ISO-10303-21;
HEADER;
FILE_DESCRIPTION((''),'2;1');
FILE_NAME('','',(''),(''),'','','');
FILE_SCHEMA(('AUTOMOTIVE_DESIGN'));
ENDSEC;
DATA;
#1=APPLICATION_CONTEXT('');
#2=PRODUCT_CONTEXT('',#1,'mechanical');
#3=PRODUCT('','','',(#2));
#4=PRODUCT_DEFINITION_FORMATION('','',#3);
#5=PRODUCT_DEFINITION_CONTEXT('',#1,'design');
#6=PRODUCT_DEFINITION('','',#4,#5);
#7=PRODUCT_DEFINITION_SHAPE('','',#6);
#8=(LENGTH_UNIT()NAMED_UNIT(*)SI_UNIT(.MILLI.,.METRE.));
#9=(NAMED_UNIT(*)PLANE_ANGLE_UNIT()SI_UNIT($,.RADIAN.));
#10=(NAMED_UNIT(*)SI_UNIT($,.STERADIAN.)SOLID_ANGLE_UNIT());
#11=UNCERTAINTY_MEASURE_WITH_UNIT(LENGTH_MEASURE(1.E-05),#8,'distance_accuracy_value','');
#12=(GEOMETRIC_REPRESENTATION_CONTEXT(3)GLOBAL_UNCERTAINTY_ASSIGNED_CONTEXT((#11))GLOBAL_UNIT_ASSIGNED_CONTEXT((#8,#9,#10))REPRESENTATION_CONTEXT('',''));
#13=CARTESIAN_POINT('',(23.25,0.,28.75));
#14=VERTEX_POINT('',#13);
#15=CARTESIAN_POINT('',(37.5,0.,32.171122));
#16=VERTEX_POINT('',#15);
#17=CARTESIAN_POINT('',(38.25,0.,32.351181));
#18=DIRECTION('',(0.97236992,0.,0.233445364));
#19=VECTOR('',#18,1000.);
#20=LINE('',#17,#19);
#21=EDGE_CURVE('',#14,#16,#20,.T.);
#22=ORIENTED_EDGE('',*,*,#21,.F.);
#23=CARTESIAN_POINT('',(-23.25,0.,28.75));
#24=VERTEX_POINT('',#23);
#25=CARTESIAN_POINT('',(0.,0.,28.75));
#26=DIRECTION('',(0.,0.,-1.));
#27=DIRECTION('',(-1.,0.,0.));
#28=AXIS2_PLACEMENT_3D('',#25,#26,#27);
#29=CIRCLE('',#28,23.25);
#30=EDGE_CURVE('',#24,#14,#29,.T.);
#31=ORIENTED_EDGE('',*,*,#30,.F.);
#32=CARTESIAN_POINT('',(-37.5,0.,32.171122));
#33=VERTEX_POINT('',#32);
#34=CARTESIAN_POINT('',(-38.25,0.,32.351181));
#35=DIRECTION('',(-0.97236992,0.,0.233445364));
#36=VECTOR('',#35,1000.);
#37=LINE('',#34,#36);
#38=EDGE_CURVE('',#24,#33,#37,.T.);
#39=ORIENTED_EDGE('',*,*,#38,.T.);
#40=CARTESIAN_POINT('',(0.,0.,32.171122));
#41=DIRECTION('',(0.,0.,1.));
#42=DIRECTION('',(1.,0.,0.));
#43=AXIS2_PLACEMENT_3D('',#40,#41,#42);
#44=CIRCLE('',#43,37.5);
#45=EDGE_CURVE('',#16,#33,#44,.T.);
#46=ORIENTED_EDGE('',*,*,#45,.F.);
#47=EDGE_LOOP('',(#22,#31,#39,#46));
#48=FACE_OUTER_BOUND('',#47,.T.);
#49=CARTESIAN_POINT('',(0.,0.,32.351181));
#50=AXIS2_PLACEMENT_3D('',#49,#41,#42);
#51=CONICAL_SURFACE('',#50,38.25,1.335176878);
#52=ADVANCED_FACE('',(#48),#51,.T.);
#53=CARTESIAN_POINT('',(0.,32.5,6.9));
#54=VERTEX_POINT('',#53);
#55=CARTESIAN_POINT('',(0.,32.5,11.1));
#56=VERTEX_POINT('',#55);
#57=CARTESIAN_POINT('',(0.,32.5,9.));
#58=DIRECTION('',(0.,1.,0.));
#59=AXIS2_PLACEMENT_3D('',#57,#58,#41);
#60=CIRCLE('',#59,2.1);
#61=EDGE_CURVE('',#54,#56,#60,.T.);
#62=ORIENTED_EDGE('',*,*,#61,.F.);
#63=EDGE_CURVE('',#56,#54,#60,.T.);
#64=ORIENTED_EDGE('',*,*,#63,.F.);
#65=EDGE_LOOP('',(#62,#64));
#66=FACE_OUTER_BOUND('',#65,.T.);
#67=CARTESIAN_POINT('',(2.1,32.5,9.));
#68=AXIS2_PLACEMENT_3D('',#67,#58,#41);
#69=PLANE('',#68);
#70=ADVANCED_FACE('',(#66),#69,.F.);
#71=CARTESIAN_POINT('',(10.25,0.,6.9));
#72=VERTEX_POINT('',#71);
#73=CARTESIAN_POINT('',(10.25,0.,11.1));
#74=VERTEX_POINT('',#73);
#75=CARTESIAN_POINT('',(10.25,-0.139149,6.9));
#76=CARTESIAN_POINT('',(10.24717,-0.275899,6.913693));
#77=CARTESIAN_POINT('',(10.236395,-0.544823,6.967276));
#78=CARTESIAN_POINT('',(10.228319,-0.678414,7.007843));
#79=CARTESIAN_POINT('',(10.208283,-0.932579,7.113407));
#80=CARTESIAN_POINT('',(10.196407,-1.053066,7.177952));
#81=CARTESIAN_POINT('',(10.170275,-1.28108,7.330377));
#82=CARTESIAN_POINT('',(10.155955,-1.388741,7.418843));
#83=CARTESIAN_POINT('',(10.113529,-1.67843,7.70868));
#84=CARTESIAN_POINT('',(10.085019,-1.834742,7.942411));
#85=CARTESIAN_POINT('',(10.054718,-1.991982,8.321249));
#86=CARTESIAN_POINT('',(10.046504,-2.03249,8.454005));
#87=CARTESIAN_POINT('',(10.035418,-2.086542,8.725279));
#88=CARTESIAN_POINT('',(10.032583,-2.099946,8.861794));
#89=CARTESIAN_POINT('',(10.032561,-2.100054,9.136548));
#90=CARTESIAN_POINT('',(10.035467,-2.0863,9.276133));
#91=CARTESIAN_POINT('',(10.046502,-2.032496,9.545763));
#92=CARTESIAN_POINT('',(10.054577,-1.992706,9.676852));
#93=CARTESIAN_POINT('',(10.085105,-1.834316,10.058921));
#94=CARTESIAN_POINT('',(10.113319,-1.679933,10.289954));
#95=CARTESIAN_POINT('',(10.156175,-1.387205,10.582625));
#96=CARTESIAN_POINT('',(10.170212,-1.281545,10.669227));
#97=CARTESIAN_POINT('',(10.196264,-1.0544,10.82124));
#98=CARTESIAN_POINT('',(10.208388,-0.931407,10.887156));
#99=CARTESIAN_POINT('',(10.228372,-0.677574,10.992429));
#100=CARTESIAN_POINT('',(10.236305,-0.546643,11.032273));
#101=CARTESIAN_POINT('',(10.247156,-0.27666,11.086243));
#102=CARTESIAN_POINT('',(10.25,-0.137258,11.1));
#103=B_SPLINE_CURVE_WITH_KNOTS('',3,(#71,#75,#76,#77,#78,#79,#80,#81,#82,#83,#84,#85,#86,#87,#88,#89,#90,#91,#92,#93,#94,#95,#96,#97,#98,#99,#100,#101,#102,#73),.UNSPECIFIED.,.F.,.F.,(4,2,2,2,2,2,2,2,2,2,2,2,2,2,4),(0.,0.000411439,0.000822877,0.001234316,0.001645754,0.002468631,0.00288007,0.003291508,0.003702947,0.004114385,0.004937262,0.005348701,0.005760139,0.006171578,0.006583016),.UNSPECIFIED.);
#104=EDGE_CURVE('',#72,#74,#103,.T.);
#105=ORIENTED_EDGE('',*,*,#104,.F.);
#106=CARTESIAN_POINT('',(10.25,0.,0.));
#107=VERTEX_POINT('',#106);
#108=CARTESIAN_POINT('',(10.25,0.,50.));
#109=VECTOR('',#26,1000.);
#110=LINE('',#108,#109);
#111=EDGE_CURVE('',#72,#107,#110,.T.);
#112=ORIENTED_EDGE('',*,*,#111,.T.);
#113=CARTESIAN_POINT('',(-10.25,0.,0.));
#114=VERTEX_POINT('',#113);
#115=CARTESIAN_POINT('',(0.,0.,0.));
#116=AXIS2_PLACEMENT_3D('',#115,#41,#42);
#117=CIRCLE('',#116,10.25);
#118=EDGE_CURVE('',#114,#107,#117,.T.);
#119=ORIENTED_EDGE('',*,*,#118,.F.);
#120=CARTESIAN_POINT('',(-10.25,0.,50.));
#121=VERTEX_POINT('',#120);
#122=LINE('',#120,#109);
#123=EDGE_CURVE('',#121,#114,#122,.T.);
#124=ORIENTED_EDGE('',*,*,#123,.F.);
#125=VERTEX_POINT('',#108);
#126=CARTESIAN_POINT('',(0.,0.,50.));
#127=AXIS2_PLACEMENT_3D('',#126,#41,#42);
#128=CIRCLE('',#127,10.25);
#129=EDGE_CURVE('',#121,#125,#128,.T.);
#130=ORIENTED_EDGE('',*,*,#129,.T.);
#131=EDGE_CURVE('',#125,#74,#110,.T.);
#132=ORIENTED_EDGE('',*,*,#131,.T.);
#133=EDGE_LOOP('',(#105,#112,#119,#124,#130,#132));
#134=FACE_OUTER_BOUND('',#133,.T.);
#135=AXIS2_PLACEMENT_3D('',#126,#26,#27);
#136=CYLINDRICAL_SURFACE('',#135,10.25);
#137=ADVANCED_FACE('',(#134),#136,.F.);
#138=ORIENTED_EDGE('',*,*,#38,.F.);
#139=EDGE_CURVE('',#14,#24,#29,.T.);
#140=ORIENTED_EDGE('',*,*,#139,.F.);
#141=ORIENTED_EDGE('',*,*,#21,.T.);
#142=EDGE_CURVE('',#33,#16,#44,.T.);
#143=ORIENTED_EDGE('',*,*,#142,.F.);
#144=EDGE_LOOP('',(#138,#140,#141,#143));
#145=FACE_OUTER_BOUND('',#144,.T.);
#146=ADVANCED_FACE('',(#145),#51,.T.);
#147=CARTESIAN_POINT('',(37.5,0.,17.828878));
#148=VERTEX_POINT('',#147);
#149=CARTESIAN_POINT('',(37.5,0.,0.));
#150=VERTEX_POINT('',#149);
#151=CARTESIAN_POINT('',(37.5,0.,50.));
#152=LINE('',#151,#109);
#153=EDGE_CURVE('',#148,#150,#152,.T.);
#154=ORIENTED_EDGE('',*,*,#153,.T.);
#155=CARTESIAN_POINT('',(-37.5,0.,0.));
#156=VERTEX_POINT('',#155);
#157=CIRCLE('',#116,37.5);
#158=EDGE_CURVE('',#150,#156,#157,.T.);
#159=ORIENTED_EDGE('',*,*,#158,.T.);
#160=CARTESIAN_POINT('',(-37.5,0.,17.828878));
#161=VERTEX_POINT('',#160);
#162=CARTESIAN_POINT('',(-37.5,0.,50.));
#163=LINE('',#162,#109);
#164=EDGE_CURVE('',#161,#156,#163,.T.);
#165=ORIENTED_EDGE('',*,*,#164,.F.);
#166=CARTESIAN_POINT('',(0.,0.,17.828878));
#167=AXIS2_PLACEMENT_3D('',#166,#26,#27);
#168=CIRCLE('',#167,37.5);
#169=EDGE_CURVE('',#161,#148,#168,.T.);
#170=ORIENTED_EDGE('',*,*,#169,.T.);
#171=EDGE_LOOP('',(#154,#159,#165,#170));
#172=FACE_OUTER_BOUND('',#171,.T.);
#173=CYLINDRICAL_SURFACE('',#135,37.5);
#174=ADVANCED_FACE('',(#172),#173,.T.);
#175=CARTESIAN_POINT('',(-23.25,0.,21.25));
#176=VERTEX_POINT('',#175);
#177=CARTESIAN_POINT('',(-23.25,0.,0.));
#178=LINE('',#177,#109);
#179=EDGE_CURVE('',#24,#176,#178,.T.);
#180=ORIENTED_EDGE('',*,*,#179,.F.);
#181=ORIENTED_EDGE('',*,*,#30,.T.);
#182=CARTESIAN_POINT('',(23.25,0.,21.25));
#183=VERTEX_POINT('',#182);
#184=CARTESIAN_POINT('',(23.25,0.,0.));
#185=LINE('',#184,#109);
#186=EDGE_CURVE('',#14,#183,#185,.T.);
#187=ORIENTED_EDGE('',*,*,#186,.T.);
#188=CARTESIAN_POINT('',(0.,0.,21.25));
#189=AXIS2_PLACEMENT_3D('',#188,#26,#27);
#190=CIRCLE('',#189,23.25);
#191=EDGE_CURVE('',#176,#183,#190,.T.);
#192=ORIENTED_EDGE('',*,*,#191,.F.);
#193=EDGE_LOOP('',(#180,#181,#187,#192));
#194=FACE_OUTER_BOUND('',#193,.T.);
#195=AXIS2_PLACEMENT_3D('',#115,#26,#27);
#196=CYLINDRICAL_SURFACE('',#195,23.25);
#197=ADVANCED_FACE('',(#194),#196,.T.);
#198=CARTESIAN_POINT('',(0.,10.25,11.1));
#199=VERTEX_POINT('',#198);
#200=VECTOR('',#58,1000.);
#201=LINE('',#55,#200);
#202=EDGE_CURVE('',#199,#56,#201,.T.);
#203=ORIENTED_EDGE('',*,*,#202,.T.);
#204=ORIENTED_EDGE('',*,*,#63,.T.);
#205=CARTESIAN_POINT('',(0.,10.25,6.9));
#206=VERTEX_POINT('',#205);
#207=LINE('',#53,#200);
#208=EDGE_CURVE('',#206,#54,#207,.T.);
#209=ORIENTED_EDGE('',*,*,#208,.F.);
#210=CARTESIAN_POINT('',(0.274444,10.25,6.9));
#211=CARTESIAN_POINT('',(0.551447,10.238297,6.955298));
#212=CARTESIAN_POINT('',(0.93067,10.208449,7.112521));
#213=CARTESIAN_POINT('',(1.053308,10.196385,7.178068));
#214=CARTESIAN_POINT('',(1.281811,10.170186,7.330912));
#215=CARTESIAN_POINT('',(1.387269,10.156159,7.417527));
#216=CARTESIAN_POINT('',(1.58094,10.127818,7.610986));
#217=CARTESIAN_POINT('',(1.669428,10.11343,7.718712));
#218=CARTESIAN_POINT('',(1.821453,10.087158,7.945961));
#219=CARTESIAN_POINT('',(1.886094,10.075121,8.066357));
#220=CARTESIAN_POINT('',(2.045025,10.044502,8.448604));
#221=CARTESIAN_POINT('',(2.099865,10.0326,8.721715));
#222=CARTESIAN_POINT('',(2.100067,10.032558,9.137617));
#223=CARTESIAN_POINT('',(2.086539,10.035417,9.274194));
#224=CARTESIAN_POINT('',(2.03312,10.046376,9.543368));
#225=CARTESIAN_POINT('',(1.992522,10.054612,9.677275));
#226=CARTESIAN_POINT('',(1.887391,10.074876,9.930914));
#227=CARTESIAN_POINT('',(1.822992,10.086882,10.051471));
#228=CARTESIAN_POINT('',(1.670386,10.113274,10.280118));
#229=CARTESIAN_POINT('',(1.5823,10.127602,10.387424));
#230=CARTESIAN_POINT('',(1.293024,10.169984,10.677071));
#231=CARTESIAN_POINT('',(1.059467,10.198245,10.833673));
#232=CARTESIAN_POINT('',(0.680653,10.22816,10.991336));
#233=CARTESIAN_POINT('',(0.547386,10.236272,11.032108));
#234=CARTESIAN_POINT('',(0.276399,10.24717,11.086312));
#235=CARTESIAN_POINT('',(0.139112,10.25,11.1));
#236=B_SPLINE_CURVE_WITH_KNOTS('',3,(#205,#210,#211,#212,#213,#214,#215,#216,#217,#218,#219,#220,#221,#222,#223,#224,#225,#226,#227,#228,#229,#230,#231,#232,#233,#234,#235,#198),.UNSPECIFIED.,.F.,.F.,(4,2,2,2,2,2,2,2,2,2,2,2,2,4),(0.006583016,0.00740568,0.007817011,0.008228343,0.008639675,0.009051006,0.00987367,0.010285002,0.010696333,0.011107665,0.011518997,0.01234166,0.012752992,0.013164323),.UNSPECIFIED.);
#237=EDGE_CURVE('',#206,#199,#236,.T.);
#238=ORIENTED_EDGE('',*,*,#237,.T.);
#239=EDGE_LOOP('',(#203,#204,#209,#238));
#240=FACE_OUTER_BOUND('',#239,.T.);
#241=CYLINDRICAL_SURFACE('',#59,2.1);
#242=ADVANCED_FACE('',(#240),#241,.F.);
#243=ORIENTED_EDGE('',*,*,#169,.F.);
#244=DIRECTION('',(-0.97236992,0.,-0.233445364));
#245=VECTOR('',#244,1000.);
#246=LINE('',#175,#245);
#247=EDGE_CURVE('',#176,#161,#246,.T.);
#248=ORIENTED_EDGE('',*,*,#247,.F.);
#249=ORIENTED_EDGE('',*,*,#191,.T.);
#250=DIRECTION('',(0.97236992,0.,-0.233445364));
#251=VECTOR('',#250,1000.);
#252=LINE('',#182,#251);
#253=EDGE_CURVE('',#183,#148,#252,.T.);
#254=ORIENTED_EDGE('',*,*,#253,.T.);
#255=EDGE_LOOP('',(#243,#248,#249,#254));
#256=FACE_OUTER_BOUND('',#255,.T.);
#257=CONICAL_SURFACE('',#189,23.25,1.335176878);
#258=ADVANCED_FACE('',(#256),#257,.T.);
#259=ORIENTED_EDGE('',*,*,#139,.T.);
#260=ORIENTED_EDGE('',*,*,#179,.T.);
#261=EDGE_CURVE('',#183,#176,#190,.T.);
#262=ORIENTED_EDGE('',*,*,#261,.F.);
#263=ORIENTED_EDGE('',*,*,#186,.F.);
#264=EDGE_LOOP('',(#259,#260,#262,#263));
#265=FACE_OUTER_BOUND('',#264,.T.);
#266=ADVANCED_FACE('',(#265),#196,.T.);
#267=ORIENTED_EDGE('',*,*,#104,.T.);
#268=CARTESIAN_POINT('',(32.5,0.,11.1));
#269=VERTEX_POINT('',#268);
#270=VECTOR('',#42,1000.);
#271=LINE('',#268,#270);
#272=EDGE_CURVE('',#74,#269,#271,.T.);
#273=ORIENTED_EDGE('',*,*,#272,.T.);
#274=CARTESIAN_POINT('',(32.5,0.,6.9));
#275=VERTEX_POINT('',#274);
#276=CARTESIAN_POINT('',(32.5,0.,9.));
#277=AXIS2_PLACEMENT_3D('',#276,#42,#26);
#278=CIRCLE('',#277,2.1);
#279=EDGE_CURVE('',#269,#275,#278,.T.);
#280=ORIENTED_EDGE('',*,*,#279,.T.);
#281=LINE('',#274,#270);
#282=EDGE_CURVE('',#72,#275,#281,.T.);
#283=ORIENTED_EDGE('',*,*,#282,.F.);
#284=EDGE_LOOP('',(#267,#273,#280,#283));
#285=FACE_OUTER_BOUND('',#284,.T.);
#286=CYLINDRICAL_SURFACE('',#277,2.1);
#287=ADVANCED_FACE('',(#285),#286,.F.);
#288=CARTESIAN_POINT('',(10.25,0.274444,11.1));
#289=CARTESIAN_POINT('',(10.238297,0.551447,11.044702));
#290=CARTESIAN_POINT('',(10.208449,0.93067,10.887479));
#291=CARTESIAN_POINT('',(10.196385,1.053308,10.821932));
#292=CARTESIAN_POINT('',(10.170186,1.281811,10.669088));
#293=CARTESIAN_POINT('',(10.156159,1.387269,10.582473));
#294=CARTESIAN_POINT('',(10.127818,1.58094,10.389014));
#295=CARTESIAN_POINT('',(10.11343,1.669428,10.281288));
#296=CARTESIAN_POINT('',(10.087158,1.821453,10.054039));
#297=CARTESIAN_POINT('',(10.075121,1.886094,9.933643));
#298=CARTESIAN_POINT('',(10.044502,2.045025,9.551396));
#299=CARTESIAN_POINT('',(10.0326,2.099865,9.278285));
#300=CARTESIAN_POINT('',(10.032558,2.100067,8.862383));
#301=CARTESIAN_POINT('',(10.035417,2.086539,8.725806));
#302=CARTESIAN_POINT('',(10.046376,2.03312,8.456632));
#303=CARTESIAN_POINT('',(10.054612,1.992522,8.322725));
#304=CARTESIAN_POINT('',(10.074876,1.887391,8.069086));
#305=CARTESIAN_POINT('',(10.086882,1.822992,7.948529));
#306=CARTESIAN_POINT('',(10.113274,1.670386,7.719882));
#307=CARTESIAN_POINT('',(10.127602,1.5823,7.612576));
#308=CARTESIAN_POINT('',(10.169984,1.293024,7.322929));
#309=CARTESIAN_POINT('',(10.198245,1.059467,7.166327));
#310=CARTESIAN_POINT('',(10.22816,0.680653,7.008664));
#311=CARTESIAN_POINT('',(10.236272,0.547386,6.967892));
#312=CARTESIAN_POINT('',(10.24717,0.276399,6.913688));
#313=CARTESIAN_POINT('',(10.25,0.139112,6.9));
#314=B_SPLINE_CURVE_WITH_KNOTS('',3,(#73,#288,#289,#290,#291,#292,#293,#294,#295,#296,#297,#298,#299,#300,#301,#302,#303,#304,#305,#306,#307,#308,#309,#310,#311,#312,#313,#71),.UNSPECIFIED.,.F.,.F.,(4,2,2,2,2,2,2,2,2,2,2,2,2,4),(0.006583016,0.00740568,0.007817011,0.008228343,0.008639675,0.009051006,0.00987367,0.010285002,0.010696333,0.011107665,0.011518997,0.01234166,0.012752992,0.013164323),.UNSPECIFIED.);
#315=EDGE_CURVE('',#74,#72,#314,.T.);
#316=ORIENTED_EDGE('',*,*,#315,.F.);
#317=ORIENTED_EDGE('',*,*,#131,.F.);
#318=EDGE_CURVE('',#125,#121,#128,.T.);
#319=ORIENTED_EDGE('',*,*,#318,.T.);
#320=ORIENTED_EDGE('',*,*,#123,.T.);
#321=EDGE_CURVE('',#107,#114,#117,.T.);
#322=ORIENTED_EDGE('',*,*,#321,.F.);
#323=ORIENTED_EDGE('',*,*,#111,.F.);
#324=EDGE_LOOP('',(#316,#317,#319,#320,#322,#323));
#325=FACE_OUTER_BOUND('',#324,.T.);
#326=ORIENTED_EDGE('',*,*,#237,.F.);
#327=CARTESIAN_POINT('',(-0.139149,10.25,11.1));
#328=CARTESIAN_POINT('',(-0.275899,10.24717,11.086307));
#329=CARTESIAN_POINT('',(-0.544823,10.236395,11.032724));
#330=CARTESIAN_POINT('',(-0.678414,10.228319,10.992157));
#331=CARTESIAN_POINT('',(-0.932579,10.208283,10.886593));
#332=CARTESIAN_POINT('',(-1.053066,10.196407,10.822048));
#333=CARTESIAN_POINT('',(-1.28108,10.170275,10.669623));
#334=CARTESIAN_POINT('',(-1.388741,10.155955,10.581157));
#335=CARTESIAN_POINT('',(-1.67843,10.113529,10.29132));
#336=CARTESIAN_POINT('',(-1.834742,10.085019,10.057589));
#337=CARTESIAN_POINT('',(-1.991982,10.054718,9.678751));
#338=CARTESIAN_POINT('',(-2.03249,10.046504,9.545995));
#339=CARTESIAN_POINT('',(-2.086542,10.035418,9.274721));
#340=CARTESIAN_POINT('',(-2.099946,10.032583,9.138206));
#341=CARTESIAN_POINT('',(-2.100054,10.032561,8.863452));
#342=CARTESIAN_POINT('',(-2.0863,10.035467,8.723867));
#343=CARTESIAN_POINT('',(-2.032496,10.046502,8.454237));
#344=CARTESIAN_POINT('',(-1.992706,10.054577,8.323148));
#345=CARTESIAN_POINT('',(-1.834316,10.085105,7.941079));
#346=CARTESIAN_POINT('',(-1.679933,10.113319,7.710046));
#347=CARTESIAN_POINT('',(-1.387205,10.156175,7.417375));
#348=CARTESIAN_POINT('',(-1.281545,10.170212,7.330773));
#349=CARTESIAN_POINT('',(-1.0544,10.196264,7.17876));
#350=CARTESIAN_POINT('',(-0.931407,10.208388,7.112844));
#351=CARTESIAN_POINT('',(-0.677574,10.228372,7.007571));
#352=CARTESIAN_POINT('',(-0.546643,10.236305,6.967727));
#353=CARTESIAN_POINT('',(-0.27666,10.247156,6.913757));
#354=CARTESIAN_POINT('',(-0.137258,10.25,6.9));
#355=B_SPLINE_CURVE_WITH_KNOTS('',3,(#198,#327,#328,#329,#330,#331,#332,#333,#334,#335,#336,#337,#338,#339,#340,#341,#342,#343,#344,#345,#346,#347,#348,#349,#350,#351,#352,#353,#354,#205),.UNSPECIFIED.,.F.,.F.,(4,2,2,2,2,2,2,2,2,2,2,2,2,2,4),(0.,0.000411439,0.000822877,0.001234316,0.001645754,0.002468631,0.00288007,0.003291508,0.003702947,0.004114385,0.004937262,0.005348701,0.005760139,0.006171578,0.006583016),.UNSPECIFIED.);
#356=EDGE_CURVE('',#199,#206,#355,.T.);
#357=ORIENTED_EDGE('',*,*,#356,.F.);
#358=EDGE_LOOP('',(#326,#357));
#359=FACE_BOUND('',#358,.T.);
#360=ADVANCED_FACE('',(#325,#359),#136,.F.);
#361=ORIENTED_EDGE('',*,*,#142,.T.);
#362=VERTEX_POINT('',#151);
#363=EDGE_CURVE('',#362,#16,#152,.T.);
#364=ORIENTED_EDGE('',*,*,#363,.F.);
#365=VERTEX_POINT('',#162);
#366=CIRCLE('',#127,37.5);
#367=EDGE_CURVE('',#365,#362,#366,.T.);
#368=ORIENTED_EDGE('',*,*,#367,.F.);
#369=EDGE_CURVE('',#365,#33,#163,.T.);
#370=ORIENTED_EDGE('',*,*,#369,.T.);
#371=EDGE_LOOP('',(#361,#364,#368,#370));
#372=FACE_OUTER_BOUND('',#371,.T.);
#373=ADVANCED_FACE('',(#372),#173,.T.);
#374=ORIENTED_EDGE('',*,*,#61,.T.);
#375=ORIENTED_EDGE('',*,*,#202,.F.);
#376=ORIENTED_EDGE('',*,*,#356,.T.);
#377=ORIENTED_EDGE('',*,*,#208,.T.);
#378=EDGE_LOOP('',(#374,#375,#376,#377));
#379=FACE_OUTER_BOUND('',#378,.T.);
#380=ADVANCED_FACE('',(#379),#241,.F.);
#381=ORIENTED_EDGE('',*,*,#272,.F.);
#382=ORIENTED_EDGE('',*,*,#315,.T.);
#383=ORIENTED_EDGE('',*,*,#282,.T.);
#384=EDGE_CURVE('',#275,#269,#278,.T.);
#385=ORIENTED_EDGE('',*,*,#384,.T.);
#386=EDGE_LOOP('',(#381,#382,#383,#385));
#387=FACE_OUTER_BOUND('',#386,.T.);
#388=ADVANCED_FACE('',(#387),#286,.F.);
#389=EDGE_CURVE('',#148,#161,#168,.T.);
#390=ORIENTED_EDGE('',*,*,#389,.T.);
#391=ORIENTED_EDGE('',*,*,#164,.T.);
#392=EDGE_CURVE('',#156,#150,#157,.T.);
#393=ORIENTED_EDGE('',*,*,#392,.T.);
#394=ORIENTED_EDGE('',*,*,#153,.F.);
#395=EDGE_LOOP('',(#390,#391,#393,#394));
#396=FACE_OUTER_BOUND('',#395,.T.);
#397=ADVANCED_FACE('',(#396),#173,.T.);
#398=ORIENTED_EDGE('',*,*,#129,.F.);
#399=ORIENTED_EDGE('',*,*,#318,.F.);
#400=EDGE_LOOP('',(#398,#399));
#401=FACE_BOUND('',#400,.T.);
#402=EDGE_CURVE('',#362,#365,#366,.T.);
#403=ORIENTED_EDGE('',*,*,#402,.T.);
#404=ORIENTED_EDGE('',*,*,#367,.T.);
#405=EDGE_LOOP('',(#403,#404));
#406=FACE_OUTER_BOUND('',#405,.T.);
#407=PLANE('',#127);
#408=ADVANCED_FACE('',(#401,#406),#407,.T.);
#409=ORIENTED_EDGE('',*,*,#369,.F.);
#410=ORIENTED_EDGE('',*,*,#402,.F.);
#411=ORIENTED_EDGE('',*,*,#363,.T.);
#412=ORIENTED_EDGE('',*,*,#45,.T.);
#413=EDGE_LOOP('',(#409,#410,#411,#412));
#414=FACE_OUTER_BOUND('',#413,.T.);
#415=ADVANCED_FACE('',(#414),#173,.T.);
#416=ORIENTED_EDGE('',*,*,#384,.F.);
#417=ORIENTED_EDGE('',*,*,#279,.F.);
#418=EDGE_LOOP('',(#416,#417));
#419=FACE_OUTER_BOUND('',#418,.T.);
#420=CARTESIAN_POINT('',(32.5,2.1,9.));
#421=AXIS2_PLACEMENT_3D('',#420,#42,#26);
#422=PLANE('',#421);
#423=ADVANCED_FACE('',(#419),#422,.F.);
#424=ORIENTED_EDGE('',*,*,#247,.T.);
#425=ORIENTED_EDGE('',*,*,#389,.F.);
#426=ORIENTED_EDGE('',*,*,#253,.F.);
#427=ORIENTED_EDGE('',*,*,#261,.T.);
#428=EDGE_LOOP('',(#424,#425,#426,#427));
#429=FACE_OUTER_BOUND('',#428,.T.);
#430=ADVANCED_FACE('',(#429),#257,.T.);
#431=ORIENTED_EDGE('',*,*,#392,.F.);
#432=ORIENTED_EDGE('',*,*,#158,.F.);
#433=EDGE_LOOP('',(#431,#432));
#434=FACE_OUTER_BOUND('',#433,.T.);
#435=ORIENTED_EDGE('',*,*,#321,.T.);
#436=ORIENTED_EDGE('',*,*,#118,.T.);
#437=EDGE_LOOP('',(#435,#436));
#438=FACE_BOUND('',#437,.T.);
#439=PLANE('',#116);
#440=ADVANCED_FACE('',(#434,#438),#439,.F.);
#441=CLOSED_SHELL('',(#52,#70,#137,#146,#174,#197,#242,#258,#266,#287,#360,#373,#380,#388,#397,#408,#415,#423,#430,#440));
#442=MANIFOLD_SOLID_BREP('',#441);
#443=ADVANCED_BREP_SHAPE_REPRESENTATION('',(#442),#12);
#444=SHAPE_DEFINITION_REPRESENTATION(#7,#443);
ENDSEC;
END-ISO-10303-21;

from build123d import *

# Parameters (mm, degrees)
SKETCH_1_R      = 37.5
SKETCH_1_R_2    = 10.25
EXTRUDE_1_DEPTH = 50


with BuildPart() as part:
    # 草图1 → 凸台-拉伸1 (new body)
    with BuildSketch(Plane.XY):
        Circle(SKETCH_1_R)
        Circle(SKETCH_1_R_2, mode=Mode.SUBTRACT)
    extrude(amount=EXTRUDE_1_DEPTH)

    # 草图2 → 切除-旋转1 (revolve, cut)
    with BuildSketch(Plane(origin=(0, 0, 0), x_dir=(1, 0, 0), z_dir=(0, 1, 0))):
        Polygon((-38.25, -17.648818614), (-23.25, -21.25), (-23.25, -28.75), (-38.25, -32.351181386), align=None)
    revolve(axis=Axis((0, 0, 0), (0, 0, 1)), mode=Mode.SUBTRACT)

    # 草图3 → M5 螺纹孔2 (revolve, cut)
    with BuildSketch(Plane(origin=(0, 32.5, 9), x_dir=(0, 0, 1), z_dir=(1, 0, 0))):
        Polygon((0, 0), (0, 31.2618073), (2.1, 30), (2.1, 0), align=None)
    revolve(axis=Axis((0, 38.85, 9), (0, -1, 0)), mode=Mode.SUBTRACT)

    # 草图5 → M5 螺纹孔1 (revolve, cut)
    with BuildSketch(Plane(origin=(32.5, 0, 9), x_dir=(0, 0, -1), z_dir=(0, 1, 0))):
        Polygon((0, 0), (0, 31.2618073), (2.1, 30), (2.1, 0), align=None)
    revolve(axis=Axis((38.85, 0, 9), (-1, 0, 0)), mode=Mode.SUBTRACT)


solid = part.part
